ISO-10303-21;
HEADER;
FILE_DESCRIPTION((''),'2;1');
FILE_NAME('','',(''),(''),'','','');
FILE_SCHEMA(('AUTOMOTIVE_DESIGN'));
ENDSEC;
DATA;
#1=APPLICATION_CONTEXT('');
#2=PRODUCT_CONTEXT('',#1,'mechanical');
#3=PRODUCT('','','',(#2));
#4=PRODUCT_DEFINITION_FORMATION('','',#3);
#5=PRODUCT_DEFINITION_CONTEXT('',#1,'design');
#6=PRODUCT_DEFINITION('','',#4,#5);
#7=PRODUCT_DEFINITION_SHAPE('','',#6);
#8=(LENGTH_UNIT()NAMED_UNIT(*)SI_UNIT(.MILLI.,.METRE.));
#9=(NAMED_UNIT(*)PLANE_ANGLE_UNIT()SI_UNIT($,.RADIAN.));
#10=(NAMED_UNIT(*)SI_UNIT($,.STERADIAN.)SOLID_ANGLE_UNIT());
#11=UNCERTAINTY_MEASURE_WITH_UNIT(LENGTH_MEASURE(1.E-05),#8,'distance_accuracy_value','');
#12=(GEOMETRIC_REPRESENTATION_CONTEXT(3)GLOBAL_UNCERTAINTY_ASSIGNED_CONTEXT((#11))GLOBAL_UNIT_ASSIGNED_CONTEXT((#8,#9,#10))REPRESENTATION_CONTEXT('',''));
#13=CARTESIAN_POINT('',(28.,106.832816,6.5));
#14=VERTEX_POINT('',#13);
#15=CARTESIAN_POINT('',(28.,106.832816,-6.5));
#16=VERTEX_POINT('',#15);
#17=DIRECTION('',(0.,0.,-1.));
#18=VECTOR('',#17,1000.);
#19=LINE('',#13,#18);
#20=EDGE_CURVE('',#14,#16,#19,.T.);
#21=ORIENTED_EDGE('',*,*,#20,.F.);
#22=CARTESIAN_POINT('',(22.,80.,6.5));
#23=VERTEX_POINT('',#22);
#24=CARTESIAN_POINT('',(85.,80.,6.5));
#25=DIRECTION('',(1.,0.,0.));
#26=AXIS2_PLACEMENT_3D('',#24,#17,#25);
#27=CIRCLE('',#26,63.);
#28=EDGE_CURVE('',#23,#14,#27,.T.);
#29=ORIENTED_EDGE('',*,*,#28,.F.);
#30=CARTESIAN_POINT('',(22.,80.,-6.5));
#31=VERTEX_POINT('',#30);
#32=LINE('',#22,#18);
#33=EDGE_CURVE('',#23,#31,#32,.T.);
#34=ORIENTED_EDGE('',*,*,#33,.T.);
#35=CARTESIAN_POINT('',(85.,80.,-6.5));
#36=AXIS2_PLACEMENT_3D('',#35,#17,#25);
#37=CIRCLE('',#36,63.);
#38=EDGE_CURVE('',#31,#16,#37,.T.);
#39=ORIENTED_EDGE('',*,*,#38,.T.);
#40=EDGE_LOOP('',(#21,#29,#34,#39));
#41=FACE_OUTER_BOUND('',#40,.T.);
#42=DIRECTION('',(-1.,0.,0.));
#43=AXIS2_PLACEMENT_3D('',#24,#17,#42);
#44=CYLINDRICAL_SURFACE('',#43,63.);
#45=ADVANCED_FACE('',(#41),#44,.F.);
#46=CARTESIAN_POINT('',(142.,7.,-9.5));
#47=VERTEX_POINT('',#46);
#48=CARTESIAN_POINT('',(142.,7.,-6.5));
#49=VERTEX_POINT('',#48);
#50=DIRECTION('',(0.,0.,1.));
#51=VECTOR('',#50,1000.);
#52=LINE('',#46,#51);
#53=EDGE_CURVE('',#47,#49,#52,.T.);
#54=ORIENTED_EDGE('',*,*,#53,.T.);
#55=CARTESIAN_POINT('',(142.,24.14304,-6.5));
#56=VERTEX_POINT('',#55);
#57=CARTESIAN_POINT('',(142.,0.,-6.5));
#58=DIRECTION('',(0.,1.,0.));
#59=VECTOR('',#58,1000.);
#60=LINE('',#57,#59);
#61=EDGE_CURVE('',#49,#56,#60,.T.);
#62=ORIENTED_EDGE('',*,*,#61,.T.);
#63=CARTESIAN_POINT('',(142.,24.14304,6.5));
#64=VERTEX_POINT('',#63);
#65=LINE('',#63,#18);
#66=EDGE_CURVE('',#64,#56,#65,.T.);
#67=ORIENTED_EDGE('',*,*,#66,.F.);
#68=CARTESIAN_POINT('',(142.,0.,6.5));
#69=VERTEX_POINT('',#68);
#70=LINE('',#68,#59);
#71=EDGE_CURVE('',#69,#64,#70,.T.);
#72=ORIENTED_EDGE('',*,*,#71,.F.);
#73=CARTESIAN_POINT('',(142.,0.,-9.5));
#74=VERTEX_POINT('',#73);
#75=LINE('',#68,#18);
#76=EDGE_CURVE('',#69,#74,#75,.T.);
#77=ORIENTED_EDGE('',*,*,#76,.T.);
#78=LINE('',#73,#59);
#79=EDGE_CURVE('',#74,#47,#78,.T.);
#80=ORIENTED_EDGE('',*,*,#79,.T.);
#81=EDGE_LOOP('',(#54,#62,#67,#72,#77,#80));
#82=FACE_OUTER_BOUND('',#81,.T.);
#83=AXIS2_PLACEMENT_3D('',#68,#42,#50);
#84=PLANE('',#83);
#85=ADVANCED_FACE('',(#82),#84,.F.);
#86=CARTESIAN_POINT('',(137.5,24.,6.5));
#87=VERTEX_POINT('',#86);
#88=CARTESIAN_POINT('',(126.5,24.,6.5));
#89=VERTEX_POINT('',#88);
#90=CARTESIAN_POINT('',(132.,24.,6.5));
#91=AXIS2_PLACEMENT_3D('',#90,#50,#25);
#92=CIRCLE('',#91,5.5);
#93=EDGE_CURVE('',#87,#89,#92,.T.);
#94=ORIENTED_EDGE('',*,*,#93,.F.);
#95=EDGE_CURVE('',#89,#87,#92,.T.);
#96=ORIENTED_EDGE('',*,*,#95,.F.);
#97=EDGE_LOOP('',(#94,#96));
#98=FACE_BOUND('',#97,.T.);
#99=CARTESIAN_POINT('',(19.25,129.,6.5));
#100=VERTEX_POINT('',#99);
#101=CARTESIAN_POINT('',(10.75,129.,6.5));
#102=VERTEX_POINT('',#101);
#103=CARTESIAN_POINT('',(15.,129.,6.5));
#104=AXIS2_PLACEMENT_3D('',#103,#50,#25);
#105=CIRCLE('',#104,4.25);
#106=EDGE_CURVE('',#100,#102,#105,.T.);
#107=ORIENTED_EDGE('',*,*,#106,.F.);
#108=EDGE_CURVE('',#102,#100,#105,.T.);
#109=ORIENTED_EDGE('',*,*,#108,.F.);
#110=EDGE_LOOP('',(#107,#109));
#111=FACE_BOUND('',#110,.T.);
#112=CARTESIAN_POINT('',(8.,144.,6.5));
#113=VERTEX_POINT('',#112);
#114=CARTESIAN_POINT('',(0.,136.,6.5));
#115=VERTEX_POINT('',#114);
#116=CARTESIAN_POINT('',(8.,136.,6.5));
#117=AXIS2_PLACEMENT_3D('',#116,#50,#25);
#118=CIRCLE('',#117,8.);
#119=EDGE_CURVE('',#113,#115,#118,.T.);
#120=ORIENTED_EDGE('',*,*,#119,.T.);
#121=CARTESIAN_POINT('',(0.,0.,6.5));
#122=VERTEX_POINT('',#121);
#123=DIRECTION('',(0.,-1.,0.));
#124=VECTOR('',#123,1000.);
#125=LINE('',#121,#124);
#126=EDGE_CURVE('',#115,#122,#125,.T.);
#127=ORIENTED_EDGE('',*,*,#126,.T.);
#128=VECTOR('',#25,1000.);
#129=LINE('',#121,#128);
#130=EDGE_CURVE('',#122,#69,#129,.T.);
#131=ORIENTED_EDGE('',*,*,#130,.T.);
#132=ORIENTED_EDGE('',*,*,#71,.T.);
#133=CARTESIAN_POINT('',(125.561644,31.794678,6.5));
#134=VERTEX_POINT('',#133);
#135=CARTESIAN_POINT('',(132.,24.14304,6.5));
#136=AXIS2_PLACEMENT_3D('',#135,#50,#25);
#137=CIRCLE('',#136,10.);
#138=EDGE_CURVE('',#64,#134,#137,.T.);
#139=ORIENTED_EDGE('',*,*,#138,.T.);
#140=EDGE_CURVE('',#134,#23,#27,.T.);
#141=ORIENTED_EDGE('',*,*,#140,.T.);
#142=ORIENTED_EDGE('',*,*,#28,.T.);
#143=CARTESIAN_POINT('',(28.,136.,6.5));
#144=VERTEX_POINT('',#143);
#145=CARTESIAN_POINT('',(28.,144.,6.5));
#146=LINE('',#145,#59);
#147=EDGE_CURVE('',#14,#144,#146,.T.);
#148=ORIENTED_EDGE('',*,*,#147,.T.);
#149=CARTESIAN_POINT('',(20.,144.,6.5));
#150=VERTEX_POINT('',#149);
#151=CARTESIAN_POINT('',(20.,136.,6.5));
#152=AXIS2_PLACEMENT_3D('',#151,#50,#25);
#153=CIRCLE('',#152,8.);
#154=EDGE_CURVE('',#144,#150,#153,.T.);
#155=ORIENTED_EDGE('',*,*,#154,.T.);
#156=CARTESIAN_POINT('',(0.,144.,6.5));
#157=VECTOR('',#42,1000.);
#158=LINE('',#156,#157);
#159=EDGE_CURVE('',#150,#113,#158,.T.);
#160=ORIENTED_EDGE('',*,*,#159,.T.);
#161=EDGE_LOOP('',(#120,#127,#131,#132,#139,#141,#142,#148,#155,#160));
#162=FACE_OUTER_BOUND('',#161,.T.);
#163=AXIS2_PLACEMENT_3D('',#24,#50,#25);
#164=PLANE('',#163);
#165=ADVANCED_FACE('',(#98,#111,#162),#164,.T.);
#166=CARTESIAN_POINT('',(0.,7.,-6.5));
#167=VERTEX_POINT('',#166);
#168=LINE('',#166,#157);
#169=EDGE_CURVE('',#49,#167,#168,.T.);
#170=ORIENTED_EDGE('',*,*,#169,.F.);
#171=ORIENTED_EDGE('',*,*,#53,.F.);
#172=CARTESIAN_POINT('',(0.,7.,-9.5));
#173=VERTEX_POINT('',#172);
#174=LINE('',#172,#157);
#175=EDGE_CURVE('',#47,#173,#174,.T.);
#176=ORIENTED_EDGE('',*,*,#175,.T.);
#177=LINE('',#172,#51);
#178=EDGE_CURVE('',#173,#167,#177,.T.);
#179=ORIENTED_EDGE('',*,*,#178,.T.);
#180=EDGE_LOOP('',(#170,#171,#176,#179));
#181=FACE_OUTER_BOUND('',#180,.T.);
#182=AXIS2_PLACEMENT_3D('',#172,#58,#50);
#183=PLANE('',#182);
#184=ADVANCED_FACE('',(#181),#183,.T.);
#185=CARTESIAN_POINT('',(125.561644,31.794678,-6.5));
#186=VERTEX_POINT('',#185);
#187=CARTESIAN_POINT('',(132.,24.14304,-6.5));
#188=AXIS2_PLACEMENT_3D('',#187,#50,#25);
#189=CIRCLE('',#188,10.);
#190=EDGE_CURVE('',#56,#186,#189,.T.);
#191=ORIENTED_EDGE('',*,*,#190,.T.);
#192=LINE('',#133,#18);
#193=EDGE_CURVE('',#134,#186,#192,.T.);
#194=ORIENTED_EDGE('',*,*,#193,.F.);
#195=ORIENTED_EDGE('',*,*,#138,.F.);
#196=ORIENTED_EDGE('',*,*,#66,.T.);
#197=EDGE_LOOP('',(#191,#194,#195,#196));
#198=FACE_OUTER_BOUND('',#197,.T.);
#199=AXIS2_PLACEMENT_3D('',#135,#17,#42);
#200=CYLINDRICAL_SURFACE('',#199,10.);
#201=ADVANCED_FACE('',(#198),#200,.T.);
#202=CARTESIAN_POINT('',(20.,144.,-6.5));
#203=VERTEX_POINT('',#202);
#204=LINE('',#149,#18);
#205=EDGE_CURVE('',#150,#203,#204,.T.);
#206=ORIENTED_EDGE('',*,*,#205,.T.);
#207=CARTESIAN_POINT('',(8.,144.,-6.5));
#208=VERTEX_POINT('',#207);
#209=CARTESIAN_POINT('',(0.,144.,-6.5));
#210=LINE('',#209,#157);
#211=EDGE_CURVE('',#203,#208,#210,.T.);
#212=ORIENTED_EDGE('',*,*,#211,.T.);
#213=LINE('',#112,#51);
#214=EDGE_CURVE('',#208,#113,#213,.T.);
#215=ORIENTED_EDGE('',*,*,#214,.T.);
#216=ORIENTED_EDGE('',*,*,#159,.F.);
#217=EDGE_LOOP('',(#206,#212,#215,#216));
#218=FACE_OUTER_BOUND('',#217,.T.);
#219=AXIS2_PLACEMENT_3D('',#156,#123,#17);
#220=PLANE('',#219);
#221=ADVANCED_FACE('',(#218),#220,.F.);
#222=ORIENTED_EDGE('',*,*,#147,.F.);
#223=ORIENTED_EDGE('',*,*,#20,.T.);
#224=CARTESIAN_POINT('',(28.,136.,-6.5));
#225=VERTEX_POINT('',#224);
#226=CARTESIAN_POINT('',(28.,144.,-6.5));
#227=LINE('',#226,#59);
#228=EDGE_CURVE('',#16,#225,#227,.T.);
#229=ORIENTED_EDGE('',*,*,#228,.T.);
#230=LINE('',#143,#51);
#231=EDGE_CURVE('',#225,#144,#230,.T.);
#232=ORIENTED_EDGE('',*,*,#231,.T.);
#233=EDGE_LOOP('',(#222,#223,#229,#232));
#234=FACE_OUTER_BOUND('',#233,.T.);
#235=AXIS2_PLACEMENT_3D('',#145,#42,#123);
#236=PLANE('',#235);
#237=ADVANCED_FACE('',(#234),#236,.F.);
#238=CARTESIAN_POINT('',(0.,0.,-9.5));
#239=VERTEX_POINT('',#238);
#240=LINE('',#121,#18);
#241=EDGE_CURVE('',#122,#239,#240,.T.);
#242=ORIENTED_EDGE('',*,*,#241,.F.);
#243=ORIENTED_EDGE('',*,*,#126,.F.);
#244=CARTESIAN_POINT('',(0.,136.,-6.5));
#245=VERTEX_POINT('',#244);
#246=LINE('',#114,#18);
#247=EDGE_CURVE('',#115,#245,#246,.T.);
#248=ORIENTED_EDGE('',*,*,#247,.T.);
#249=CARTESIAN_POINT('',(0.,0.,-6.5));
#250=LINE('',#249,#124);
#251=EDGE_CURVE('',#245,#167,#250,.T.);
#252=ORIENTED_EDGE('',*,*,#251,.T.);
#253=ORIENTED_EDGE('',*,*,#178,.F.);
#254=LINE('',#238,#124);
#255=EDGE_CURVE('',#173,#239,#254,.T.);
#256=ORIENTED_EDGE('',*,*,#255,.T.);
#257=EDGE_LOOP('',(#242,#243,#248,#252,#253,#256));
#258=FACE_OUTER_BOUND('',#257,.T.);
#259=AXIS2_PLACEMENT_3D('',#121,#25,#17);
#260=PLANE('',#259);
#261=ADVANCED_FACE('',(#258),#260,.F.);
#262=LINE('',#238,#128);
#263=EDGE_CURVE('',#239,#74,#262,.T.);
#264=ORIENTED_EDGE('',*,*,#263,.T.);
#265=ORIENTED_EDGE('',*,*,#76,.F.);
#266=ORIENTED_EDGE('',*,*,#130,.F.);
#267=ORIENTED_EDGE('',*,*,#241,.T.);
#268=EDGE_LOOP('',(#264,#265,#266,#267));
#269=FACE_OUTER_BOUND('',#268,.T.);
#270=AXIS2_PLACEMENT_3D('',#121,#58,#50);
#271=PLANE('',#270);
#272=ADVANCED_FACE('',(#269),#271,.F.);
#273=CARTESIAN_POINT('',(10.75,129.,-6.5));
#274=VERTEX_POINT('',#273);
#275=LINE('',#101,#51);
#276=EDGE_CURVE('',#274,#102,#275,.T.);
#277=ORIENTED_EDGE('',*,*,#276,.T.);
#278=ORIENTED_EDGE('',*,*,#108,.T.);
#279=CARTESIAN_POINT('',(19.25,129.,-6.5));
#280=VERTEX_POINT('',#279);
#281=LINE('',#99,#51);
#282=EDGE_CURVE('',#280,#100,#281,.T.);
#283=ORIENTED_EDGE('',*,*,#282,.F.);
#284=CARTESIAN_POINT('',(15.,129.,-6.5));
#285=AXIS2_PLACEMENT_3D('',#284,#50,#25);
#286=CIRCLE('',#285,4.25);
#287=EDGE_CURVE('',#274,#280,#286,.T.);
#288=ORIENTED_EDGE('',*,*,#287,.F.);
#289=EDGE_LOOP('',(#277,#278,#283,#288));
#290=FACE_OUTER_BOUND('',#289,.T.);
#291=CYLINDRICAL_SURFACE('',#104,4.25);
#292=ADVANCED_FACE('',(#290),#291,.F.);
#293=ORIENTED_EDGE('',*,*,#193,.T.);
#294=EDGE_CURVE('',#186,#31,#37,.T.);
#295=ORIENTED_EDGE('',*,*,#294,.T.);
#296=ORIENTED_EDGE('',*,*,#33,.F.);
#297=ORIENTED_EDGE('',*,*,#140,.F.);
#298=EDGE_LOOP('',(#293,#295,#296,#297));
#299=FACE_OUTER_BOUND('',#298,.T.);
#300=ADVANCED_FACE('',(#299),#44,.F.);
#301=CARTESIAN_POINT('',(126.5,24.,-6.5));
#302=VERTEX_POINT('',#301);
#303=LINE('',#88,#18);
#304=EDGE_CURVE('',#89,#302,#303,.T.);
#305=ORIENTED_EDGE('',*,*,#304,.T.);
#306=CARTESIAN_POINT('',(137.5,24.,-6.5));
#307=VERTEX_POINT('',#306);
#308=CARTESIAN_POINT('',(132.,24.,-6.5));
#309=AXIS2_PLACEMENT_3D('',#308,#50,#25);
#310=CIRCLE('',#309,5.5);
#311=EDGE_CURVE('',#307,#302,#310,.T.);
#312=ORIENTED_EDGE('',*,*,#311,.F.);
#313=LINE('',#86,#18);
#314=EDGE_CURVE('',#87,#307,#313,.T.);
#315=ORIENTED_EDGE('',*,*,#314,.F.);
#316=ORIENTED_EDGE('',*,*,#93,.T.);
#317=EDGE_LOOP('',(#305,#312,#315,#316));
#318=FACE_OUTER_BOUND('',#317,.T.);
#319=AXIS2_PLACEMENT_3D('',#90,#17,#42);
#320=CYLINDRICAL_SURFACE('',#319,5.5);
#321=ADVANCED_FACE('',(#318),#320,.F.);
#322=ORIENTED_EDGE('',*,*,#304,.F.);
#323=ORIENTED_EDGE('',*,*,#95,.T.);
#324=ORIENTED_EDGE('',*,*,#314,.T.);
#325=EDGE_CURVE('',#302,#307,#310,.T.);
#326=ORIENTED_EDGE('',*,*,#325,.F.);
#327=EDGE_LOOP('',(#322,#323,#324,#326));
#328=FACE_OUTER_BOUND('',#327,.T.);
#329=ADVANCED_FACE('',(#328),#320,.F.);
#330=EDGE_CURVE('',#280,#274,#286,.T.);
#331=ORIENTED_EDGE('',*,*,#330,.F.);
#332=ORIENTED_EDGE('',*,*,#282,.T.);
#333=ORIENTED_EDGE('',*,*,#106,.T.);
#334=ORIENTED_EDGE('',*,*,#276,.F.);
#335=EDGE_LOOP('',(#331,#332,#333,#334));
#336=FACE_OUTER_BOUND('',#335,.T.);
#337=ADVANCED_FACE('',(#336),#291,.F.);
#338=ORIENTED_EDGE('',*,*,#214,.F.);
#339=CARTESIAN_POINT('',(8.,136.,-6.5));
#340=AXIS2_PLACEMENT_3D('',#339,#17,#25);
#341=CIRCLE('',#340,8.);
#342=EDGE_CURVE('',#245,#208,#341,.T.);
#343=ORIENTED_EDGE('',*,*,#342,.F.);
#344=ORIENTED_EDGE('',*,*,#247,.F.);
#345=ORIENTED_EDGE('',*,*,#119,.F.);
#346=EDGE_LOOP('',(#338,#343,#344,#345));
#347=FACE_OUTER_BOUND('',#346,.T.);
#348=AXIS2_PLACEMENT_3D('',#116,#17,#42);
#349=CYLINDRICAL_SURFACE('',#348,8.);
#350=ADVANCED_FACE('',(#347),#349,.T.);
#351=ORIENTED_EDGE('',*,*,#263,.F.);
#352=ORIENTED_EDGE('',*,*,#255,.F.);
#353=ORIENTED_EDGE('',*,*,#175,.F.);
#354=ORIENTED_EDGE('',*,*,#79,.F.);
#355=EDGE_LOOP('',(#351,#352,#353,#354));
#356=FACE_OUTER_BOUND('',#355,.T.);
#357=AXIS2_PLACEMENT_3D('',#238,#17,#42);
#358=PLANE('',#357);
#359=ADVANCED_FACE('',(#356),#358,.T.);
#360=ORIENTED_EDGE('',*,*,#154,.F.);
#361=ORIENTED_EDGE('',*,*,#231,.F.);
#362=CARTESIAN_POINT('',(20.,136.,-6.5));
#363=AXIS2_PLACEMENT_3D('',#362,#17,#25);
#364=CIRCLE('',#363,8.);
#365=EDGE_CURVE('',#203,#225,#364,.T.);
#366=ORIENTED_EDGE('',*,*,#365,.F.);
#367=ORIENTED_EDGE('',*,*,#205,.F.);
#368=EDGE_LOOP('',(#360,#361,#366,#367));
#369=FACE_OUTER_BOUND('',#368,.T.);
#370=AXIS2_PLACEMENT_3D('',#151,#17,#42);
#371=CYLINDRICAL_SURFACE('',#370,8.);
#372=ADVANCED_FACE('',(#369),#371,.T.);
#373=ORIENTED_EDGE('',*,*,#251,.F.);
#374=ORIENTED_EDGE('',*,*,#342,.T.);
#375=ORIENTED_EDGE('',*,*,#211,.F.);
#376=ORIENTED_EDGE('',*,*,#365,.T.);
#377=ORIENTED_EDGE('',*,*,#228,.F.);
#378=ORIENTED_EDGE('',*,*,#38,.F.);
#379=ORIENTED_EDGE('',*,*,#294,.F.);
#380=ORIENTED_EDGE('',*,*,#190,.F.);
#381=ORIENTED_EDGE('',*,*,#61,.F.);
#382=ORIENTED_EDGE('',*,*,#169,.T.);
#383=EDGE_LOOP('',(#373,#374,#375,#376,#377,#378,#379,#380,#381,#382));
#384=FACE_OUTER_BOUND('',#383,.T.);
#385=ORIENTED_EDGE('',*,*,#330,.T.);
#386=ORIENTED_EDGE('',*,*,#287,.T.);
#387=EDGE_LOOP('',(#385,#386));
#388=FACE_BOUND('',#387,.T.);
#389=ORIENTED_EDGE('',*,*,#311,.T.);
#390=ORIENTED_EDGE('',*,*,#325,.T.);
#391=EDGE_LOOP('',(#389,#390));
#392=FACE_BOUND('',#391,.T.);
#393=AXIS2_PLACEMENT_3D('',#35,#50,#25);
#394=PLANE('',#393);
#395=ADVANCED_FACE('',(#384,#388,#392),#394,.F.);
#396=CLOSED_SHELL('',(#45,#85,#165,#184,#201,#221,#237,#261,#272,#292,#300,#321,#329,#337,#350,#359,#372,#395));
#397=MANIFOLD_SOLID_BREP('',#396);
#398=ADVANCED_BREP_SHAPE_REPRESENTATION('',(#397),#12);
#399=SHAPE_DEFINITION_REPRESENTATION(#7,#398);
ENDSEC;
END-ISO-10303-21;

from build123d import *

# Parameters (mm, degrees)
SKETCH1_R           = 5.5
BOSS_EXTRUDE1_DEPTH = 6.5
SKETCH2_W           = 142
SKETCH2_H           = 7
BOSS_EXTRUDE2_DEPTH = 3
M10_TAPPED_HOLE1_D  = 8.5
FILLET1_R           = 8


with BuildPart() as part:
    # Sketch1 → Boss-Extrude1 (new, symmetric)
    with BuildSketch(Plane.XY):
        with BuildLine():
            Line((28, 144), (28, 106.83281573))
            ThreePointArc((28, 106.83281573), (46.591206617, 30.06239302), (125.561643836, 31.794678205))
            ThreePointArc((125.561643836, 31.794678205), (136.219978576, 33.209008103), (142, 24.143039825))
            Line((142, 24.143039825), (142, 0))
            Line((142, 0), (0, 0))
            Line((0, 0), (0, 144))
            Line((0, 144), (28, 144))
        make_face()
        with Locations(Location((132, 24, 0), (0, 0, 180))):
            Circle(SKETCH1_R, mode=Mode.SUBTRACT)
    extrude(amount=BOSS_EXTRUDE1_DEPTH, both=True)

    # Sketch2 → Boss-Extrude2 (add)
    with BuildSketch(Plane.XY.offset(-6.5)):
        with Locations((71, 3.5)):
            Rectangle(SKETCH2_W, SKETCH2_H)
    extrude(amount=-BOSS_EXTRUDE2_DEPTH)

    # M10 Tapped Hole1 (through all)
    with Locations(Plane.XY.offset(6.5)):
        with Locations((15, 129)):
            Hole(M10_TAPPED_HOLE1_D / 2)

    # Fillet1
    fillet1_edges = [part.edges().sort_by_distance(p)[0] for p in [
        (0, 144, 0),
        (28, 144, 0),
    ]]
    fillet(fillet1_edges, radius=FILLET1_R)


solid = part.part
